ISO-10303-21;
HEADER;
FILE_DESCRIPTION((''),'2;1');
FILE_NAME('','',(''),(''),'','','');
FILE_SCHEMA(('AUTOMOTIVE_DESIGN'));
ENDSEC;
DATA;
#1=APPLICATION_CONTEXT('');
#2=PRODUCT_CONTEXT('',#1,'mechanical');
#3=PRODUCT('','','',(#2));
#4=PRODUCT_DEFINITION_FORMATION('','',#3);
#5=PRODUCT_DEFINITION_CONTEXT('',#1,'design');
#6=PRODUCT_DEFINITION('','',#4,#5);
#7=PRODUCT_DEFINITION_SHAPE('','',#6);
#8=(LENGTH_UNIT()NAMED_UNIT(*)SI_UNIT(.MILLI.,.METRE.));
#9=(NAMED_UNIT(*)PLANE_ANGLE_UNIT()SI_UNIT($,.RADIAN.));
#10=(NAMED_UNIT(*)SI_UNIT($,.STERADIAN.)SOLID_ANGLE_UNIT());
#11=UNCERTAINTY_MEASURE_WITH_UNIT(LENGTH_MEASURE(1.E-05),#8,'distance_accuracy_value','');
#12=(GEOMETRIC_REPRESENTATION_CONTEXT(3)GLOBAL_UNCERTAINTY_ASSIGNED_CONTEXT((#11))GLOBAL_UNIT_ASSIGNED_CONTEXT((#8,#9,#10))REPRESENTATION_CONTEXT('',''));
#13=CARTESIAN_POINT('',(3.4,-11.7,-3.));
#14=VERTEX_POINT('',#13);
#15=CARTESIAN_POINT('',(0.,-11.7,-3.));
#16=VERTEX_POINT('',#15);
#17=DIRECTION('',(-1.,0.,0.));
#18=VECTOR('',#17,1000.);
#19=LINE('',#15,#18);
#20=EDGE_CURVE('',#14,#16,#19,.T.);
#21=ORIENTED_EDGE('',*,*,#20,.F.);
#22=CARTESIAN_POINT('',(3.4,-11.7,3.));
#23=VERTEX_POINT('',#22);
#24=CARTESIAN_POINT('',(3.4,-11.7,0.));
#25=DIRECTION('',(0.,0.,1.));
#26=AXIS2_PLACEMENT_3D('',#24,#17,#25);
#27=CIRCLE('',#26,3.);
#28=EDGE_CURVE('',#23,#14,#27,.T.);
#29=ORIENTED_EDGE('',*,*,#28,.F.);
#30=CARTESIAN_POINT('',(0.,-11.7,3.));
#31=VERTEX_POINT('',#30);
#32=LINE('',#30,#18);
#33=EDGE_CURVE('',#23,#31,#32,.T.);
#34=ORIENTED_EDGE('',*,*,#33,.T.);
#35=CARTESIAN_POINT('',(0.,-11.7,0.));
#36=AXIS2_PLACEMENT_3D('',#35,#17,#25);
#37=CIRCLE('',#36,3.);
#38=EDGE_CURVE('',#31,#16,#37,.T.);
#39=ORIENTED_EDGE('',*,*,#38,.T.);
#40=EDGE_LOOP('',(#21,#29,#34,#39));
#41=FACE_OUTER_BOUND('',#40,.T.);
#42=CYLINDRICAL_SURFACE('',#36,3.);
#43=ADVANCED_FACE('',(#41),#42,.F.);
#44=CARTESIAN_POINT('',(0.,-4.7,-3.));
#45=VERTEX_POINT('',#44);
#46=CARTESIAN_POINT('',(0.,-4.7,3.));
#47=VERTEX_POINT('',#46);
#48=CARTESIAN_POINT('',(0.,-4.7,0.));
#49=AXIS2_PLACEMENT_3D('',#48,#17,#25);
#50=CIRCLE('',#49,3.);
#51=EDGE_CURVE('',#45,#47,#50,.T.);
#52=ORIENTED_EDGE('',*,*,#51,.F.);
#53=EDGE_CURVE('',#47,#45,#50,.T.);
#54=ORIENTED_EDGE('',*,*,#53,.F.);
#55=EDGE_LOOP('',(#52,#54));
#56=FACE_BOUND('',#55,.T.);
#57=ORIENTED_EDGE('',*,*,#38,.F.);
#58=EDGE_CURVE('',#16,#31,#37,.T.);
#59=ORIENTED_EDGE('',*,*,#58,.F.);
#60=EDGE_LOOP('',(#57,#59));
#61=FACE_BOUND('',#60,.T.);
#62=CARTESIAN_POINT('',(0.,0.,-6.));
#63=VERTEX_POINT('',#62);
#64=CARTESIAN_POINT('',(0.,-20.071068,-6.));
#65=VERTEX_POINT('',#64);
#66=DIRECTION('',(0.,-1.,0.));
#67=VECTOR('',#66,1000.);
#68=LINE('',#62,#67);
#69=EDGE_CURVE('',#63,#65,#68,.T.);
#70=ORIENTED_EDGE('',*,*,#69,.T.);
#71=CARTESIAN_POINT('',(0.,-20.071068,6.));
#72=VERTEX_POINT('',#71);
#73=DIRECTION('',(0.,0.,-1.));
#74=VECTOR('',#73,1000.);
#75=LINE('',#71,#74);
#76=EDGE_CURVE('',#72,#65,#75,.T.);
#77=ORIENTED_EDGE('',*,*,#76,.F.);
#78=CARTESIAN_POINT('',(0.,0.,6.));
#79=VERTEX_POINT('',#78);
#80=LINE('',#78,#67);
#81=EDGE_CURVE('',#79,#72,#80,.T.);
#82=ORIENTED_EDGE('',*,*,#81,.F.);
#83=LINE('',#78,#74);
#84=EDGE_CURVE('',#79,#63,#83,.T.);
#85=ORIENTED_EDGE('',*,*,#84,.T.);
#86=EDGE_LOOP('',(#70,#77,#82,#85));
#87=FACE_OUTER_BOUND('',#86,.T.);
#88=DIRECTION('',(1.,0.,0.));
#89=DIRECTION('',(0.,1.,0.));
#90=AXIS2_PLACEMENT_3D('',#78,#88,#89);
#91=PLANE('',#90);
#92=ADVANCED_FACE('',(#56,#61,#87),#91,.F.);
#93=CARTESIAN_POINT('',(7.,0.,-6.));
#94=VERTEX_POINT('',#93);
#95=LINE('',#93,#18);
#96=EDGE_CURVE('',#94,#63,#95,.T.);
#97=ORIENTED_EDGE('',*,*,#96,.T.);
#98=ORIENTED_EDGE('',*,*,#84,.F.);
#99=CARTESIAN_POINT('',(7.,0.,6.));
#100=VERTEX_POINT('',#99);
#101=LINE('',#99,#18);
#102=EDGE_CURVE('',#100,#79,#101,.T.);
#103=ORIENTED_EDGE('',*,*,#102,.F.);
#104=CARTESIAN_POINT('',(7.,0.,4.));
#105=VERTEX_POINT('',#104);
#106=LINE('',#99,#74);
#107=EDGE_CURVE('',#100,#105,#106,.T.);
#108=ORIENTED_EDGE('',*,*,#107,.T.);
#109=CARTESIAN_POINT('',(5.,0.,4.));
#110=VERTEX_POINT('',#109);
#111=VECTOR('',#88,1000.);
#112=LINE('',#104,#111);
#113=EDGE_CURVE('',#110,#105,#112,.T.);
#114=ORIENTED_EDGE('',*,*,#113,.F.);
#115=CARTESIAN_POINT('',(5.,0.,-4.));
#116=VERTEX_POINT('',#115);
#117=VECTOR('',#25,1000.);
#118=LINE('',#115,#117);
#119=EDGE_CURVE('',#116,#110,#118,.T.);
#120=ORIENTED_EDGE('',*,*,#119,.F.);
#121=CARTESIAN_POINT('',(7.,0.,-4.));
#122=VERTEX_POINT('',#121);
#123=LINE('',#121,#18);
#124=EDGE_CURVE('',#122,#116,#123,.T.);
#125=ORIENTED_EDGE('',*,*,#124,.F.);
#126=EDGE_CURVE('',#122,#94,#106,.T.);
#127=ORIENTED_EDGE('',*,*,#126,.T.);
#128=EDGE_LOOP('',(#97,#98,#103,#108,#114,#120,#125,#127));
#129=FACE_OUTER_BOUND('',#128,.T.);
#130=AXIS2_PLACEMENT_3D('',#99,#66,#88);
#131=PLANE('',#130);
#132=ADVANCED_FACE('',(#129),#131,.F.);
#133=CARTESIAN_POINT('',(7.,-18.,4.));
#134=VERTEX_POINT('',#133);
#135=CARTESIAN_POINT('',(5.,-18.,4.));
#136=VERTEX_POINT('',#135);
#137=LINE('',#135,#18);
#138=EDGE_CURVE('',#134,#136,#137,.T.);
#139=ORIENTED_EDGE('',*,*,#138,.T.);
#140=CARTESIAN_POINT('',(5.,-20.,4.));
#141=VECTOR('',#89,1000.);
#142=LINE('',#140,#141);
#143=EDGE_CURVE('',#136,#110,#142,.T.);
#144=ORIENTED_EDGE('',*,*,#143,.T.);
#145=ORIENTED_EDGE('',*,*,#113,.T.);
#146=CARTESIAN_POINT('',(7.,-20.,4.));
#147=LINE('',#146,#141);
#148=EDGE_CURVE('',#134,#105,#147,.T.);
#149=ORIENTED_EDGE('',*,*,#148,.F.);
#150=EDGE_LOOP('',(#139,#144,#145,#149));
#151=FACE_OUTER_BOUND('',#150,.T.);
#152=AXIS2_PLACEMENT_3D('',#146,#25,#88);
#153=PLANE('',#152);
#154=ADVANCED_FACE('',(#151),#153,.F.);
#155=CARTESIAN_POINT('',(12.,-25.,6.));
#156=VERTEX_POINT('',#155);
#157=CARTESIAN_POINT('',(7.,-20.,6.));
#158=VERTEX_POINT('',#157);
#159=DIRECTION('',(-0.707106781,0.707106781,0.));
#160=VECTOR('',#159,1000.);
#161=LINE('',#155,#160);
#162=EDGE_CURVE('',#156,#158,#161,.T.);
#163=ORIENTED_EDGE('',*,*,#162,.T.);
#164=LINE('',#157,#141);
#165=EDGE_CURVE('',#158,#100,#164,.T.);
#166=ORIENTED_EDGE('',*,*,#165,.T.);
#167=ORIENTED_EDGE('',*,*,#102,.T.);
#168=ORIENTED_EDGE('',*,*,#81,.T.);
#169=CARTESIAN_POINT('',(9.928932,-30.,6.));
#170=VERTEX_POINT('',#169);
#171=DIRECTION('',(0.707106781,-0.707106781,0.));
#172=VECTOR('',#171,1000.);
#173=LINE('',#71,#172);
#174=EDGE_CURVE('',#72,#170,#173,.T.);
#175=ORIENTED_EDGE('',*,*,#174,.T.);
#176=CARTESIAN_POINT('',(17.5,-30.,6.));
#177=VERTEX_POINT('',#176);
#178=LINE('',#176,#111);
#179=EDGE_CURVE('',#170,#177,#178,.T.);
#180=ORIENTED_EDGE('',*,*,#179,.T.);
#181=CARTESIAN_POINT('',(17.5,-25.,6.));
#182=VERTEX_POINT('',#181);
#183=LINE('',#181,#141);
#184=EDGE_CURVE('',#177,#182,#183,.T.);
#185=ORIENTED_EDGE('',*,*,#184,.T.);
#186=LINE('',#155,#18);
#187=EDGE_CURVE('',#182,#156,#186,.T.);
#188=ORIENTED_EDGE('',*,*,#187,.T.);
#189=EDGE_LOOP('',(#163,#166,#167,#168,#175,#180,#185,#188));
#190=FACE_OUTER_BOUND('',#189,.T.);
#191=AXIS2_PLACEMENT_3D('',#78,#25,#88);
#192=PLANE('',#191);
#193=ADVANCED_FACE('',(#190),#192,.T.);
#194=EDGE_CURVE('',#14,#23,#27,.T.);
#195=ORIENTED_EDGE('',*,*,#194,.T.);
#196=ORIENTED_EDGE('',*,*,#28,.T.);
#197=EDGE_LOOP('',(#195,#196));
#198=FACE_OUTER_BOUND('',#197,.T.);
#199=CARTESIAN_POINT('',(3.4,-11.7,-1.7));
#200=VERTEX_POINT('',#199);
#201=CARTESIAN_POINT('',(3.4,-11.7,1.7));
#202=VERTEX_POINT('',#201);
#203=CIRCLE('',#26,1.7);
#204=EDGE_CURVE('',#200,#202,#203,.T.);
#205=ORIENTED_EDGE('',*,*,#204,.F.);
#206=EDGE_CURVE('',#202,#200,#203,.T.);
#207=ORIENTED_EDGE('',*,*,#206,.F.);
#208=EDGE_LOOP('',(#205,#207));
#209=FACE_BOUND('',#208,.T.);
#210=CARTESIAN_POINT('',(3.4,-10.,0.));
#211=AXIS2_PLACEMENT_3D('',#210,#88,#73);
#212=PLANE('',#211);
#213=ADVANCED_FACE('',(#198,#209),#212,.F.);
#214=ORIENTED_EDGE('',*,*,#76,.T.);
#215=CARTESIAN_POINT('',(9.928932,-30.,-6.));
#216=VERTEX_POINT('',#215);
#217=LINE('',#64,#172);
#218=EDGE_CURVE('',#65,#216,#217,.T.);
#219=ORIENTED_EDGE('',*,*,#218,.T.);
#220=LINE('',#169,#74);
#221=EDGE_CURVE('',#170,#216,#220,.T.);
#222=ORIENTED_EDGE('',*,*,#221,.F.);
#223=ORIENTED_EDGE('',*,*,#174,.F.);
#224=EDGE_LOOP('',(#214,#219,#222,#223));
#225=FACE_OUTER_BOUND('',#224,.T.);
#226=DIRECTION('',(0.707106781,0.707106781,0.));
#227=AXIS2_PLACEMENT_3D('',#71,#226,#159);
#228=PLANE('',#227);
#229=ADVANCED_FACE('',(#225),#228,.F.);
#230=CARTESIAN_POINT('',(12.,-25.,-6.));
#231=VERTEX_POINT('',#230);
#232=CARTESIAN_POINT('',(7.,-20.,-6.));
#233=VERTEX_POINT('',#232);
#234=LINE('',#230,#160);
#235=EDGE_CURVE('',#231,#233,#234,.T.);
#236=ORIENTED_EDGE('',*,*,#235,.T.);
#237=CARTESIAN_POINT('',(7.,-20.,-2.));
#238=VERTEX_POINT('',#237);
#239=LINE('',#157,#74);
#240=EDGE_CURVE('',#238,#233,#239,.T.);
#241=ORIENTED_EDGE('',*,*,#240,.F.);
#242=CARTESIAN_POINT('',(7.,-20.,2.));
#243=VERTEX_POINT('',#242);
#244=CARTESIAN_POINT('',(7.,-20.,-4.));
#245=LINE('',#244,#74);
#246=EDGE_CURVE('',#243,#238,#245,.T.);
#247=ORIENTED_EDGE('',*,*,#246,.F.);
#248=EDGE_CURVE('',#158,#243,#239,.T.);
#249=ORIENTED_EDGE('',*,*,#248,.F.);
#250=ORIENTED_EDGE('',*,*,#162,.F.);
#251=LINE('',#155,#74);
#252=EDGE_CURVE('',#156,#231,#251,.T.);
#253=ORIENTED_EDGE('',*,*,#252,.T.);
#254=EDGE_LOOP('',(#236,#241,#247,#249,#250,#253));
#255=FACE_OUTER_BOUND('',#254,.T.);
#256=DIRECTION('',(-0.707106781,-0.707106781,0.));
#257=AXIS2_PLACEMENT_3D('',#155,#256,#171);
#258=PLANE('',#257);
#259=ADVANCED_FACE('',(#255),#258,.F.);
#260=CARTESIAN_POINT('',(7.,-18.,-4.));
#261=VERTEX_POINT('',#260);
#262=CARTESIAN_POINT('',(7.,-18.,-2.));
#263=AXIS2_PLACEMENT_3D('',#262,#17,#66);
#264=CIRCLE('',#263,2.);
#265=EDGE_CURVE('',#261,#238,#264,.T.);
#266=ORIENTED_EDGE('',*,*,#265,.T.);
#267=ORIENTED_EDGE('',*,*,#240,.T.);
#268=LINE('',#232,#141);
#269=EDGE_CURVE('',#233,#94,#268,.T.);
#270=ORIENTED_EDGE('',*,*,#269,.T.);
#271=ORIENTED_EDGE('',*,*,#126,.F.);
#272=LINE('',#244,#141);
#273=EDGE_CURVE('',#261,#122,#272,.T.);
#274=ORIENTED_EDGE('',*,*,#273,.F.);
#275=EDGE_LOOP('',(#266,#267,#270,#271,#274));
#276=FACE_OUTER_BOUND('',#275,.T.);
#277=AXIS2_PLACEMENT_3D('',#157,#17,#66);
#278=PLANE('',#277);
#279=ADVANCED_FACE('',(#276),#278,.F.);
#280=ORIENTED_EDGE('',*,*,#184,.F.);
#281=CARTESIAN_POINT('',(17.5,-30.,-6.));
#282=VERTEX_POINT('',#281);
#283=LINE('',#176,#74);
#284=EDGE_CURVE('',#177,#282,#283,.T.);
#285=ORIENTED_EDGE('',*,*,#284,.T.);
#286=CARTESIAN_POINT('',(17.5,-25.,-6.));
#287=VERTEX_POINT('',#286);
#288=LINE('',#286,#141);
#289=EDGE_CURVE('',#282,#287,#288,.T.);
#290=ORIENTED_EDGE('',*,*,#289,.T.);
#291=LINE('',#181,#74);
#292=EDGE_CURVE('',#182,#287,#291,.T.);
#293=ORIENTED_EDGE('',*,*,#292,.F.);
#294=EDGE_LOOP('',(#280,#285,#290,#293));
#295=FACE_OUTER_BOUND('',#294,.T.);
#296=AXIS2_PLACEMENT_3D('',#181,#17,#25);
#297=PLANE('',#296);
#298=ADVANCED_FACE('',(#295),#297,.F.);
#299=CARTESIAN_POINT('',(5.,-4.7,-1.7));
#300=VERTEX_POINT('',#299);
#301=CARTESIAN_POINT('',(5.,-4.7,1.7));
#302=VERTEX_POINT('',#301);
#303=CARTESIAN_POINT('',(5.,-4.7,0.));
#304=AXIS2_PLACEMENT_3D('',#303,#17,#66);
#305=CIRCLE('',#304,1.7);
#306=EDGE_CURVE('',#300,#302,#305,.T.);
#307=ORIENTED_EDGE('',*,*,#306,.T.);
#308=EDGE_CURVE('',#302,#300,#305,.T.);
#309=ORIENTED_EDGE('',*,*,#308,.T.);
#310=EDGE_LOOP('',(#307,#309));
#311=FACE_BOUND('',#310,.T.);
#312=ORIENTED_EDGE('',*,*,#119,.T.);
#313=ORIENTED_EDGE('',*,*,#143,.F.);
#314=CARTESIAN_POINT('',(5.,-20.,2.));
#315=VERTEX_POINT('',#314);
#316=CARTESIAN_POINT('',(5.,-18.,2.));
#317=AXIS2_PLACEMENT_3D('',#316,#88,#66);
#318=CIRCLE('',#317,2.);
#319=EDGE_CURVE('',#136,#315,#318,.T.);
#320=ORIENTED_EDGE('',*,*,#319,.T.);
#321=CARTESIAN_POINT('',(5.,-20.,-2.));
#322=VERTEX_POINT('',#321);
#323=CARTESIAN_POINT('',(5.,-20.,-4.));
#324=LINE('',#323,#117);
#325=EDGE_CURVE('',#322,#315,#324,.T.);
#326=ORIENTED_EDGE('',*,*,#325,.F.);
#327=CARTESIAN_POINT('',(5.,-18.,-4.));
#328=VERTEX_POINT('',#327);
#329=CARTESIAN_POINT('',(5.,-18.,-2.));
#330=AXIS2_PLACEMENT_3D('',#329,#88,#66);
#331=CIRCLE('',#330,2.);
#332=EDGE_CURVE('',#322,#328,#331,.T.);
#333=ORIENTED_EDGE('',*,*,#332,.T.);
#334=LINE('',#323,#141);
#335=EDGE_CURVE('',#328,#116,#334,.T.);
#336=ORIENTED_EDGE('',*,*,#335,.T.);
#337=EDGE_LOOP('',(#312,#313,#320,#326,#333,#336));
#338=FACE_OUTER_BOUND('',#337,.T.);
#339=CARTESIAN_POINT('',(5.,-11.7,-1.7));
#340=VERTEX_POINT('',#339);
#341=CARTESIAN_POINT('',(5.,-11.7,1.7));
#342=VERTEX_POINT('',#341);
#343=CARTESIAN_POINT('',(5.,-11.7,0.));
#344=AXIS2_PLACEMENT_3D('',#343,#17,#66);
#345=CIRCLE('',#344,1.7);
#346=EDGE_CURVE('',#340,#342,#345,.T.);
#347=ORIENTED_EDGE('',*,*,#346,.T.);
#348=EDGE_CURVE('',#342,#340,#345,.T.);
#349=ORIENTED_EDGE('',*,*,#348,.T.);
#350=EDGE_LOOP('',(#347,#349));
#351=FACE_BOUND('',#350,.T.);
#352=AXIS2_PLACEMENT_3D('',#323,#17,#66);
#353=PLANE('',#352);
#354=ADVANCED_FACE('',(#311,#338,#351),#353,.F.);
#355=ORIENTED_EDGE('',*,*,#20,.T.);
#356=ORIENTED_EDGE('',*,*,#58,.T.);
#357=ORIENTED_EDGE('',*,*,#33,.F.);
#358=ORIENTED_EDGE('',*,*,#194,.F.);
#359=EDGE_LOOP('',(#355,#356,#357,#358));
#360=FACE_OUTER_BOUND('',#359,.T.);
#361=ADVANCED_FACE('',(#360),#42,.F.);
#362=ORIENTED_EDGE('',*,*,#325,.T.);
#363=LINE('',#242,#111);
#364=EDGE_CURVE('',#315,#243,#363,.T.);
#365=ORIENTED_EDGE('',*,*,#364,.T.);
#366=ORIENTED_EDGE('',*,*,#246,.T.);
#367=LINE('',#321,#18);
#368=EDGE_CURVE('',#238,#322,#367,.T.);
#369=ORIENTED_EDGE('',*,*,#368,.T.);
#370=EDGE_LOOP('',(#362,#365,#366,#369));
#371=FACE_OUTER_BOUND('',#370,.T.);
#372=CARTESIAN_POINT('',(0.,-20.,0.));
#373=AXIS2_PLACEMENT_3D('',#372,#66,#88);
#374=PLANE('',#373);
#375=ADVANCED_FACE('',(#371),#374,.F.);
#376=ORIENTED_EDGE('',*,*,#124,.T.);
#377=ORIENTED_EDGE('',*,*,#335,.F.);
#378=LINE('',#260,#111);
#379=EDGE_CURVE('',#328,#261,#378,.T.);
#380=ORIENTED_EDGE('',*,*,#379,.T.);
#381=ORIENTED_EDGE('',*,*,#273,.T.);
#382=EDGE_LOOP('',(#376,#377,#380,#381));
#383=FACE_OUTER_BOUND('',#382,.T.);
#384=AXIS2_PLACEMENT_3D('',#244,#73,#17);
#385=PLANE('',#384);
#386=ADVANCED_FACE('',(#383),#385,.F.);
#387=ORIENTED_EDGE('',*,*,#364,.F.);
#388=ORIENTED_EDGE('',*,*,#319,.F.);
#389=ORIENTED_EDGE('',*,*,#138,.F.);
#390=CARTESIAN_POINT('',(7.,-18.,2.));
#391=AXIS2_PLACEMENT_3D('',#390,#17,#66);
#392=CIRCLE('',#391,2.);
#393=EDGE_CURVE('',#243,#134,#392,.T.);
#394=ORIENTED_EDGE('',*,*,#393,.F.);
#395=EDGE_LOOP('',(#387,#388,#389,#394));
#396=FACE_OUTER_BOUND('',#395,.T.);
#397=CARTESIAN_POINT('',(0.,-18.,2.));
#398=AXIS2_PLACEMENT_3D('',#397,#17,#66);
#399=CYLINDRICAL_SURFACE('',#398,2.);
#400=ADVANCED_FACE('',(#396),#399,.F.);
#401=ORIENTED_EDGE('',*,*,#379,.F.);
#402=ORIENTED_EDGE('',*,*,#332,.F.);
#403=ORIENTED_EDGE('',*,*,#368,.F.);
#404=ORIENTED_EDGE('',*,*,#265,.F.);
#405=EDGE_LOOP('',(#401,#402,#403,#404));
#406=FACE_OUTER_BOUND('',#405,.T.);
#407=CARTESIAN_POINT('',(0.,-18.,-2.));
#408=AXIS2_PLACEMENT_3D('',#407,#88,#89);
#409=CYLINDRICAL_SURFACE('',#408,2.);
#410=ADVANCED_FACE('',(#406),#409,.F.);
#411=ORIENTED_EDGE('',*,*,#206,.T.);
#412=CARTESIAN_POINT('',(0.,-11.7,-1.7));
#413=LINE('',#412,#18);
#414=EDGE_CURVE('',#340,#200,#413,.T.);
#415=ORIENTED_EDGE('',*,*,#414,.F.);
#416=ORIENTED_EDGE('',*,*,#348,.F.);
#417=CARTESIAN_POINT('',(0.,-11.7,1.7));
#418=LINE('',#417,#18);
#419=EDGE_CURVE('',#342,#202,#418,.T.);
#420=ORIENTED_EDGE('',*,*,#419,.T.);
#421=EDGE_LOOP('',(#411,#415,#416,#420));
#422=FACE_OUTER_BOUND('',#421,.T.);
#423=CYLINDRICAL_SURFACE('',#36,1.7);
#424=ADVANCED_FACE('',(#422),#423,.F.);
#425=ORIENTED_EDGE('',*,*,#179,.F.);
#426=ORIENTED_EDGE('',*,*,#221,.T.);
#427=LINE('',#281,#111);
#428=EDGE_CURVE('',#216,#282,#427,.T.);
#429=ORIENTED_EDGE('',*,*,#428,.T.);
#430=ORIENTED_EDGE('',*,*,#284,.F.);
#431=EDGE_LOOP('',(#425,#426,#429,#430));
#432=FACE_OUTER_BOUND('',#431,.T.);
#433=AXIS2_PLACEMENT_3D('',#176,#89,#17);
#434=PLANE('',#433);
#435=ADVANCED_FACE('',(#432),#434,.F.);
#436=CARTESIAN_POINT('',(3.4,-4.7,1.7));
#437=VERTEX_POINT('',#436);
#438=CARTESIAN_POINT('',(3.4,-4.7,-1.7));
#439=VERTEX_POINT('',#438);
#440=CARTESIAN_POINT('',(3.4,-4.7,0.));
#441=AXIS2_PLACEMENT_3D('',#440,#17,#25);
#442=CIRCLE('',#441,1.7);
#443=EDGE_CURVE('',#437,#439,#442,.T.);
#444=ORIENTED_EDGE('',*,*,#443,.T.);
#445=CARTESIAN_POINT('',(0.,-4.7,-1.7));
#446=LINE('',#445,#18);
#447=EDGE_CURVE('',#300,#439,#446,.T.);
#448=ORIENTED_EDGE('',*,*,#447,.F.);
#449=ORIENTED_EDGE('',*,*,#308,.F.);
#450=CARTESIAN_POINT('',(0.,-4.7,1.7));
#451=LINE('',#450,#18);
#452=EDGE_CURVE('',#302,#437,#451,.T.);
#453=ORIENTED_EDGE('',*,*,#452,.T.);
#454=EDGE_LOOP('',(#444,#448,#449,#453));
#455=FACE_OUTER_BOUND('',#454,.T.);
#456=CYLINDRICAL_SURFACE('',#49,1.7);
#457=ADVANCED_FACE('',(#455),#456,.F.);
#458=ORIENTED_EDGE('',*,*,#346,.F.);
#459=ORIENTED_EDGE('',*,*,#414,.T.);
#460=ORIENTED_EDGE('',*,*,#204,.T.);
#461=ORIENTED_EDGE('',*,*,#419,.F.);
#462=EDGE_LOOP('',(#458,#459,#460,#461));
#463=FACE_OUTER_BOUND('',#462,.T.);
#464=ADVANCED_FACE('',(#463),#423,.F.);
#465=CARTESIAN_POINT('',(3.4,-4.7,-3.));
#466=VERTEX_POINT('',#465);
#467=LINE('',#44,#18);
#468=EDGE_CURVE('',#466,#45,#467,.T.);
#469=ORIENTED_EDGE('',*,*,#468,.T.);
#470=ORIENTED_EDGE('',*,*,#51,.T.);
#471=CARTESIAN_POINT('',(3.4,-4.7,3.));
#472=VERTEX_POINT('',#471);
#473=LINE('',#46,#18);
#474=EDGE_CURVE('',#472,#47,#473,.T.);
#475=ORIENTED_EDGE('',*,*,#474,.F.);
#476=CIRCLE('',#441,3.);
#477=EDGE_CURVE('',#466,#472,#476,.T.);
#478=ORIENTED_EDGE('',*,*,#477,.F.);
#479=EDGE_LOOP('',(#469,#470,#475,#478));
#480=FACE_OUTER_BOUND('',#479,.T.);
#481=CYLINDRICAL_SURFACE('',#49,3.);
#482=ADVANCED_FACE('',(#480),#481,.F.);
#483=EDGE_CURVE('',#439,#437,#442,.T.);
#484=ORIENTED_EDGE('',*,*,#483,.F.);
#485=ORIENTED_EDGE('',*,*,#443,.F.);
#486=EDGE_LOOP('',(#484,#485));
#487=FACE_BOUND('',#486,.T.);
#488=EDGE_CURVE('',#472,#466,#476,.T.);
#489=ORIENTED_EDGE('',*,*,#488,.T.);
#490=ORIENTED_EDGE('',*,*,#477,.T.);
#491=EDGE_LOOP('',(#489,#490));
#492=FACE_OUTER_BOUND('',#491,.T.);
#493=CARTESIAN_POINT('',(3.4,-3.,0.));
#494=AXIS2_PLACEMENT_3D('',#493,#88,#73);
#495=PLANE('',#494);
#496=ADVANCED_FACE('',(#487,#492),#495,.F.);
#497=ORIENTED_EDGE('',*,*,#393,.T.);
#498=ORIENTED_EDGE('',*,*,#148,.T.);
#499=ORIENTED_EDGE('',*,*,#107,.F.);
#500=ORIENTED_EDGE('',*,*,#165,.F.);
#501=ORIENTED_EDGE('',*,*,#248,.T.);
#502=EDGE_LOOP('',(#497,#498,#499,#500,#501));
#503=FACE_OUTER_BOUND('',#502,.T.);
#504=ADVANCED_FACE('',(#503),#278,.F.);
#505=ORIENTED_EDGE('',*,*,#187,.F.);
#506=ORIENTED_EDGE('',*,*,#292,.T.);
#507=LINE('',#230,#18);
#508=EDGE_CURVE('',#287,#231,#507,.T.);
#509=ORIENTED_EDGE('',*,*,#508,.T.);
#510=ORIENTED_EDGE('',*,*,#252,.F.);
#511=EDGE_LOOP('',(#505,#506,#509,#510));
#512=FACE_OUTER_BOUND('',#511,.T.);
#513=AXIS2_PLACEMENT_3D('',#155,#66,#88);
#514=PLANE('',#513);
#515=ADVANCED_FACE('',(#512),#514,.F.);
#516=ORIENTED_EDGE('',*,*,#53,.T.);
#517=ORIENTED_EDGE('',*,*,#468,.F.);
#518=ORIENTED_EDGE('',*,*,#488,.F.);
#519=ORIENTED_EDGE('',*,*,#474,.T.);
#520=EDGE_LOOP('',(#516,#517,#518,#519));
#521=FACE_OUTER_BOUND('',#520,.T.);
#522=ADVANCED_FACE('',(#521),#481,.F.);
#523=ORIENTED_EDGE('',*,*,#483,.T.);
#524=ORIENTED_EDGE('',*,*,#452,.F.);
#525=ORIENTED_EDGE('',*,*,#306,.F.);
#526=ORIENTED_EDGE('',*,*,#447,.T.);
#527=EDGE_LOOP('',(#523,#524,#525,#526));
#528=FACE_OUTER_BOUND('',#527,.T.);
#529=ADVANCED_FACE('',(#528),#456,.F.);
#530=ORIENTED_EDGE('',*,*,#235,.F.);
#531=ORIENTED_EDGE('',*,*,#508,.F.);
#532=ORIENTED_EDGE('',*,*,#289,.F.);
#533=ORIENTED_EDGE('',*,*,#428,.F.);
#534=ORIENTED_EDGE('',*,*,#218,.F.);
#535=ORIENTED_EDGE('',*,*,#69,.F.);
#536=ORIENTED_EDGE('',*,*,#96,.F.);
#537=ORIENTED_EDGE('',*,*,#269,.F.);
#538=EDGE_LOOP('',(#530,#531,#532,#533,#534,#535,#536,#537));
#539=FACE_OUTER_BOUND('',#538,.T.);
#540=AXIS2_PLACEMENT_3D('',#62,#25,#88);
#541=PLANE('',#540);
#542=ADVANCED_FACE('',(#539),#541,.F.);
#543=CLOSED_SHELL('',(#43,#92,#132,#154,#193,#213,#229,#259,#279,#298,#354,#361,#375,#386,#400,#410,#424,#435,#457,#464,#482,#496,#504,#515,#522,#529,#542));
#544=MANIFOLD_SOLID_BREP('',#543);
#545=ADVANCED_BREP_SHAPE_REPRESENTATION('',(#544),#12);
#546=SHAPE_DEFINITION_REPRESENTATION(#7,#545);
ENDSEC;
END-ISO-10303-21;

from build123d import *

# Parameters (mm, degrees)
EXTRUDE_1_DEPTH              = 6
SKETCH_2_W                   = 2
SKETCH_2_H                   = 8
CUT_EXTRUDE_1_DEPTH          = 20
FILLET_1_R                   = 2
HOLE_WIZARD_M3_1_D           = 3.4
HOLE_WIZARD_M3_1_CBORE_D     = 6
HOLE_WIZARD_M3_1_CBORE_DEPTH = 3.4


with BuildPart() as part:
    # 草图1 → 凸台-拉伸1 (new, symmetric)
    with BuildSketch(Plane.XY):
        Polygon((0, 0), (0, -20.071067812), (9.928932188, -30), (17.5, -30), (17.5, -25), (12, -25), (7, -20), (7, 0), align=None)
    extrude(amount=EXTRUDE_1_DEPTH, both=True)

    # 草图2 → 切除-拉伸1 (cut)
    with BuildSketch(Plane(origin=(0, 0, 0), x_dir=(1, 0, 0), z_dir=(0, 1, 0))):
        with Locations((6, 0)):
            Rectangle(SKETCH_2_W, SKETCH_2_H)
    extrude(amount=-CUT_EXTRUDE_1_DEPTH, mode=Mode.SUBTRACT)

    # 圆角1
    fillet_1_edges = [part.edges().sort_by_distance(p)[0] for p in [
        (6, -20, 4),
        (6, -20, -4),
    ]]
    fillet(fillet_1_edges, radius=FILLET_1_R)

    # M3 六角圆柱头螺钉的柱形沉头孔1 (through all)
    with Locations(Plane.ZY):
        with Locations((0, -4.7), (0, -11.7)):
            CounterBoreHole(HOLE_WIZARD_M3_1_D / 2, HOLE_WIZARD_M3_1_CBORE_D / 2, HOLE_WIZARD_M3_1_CBORE_DEPTH)


solid = part.part
